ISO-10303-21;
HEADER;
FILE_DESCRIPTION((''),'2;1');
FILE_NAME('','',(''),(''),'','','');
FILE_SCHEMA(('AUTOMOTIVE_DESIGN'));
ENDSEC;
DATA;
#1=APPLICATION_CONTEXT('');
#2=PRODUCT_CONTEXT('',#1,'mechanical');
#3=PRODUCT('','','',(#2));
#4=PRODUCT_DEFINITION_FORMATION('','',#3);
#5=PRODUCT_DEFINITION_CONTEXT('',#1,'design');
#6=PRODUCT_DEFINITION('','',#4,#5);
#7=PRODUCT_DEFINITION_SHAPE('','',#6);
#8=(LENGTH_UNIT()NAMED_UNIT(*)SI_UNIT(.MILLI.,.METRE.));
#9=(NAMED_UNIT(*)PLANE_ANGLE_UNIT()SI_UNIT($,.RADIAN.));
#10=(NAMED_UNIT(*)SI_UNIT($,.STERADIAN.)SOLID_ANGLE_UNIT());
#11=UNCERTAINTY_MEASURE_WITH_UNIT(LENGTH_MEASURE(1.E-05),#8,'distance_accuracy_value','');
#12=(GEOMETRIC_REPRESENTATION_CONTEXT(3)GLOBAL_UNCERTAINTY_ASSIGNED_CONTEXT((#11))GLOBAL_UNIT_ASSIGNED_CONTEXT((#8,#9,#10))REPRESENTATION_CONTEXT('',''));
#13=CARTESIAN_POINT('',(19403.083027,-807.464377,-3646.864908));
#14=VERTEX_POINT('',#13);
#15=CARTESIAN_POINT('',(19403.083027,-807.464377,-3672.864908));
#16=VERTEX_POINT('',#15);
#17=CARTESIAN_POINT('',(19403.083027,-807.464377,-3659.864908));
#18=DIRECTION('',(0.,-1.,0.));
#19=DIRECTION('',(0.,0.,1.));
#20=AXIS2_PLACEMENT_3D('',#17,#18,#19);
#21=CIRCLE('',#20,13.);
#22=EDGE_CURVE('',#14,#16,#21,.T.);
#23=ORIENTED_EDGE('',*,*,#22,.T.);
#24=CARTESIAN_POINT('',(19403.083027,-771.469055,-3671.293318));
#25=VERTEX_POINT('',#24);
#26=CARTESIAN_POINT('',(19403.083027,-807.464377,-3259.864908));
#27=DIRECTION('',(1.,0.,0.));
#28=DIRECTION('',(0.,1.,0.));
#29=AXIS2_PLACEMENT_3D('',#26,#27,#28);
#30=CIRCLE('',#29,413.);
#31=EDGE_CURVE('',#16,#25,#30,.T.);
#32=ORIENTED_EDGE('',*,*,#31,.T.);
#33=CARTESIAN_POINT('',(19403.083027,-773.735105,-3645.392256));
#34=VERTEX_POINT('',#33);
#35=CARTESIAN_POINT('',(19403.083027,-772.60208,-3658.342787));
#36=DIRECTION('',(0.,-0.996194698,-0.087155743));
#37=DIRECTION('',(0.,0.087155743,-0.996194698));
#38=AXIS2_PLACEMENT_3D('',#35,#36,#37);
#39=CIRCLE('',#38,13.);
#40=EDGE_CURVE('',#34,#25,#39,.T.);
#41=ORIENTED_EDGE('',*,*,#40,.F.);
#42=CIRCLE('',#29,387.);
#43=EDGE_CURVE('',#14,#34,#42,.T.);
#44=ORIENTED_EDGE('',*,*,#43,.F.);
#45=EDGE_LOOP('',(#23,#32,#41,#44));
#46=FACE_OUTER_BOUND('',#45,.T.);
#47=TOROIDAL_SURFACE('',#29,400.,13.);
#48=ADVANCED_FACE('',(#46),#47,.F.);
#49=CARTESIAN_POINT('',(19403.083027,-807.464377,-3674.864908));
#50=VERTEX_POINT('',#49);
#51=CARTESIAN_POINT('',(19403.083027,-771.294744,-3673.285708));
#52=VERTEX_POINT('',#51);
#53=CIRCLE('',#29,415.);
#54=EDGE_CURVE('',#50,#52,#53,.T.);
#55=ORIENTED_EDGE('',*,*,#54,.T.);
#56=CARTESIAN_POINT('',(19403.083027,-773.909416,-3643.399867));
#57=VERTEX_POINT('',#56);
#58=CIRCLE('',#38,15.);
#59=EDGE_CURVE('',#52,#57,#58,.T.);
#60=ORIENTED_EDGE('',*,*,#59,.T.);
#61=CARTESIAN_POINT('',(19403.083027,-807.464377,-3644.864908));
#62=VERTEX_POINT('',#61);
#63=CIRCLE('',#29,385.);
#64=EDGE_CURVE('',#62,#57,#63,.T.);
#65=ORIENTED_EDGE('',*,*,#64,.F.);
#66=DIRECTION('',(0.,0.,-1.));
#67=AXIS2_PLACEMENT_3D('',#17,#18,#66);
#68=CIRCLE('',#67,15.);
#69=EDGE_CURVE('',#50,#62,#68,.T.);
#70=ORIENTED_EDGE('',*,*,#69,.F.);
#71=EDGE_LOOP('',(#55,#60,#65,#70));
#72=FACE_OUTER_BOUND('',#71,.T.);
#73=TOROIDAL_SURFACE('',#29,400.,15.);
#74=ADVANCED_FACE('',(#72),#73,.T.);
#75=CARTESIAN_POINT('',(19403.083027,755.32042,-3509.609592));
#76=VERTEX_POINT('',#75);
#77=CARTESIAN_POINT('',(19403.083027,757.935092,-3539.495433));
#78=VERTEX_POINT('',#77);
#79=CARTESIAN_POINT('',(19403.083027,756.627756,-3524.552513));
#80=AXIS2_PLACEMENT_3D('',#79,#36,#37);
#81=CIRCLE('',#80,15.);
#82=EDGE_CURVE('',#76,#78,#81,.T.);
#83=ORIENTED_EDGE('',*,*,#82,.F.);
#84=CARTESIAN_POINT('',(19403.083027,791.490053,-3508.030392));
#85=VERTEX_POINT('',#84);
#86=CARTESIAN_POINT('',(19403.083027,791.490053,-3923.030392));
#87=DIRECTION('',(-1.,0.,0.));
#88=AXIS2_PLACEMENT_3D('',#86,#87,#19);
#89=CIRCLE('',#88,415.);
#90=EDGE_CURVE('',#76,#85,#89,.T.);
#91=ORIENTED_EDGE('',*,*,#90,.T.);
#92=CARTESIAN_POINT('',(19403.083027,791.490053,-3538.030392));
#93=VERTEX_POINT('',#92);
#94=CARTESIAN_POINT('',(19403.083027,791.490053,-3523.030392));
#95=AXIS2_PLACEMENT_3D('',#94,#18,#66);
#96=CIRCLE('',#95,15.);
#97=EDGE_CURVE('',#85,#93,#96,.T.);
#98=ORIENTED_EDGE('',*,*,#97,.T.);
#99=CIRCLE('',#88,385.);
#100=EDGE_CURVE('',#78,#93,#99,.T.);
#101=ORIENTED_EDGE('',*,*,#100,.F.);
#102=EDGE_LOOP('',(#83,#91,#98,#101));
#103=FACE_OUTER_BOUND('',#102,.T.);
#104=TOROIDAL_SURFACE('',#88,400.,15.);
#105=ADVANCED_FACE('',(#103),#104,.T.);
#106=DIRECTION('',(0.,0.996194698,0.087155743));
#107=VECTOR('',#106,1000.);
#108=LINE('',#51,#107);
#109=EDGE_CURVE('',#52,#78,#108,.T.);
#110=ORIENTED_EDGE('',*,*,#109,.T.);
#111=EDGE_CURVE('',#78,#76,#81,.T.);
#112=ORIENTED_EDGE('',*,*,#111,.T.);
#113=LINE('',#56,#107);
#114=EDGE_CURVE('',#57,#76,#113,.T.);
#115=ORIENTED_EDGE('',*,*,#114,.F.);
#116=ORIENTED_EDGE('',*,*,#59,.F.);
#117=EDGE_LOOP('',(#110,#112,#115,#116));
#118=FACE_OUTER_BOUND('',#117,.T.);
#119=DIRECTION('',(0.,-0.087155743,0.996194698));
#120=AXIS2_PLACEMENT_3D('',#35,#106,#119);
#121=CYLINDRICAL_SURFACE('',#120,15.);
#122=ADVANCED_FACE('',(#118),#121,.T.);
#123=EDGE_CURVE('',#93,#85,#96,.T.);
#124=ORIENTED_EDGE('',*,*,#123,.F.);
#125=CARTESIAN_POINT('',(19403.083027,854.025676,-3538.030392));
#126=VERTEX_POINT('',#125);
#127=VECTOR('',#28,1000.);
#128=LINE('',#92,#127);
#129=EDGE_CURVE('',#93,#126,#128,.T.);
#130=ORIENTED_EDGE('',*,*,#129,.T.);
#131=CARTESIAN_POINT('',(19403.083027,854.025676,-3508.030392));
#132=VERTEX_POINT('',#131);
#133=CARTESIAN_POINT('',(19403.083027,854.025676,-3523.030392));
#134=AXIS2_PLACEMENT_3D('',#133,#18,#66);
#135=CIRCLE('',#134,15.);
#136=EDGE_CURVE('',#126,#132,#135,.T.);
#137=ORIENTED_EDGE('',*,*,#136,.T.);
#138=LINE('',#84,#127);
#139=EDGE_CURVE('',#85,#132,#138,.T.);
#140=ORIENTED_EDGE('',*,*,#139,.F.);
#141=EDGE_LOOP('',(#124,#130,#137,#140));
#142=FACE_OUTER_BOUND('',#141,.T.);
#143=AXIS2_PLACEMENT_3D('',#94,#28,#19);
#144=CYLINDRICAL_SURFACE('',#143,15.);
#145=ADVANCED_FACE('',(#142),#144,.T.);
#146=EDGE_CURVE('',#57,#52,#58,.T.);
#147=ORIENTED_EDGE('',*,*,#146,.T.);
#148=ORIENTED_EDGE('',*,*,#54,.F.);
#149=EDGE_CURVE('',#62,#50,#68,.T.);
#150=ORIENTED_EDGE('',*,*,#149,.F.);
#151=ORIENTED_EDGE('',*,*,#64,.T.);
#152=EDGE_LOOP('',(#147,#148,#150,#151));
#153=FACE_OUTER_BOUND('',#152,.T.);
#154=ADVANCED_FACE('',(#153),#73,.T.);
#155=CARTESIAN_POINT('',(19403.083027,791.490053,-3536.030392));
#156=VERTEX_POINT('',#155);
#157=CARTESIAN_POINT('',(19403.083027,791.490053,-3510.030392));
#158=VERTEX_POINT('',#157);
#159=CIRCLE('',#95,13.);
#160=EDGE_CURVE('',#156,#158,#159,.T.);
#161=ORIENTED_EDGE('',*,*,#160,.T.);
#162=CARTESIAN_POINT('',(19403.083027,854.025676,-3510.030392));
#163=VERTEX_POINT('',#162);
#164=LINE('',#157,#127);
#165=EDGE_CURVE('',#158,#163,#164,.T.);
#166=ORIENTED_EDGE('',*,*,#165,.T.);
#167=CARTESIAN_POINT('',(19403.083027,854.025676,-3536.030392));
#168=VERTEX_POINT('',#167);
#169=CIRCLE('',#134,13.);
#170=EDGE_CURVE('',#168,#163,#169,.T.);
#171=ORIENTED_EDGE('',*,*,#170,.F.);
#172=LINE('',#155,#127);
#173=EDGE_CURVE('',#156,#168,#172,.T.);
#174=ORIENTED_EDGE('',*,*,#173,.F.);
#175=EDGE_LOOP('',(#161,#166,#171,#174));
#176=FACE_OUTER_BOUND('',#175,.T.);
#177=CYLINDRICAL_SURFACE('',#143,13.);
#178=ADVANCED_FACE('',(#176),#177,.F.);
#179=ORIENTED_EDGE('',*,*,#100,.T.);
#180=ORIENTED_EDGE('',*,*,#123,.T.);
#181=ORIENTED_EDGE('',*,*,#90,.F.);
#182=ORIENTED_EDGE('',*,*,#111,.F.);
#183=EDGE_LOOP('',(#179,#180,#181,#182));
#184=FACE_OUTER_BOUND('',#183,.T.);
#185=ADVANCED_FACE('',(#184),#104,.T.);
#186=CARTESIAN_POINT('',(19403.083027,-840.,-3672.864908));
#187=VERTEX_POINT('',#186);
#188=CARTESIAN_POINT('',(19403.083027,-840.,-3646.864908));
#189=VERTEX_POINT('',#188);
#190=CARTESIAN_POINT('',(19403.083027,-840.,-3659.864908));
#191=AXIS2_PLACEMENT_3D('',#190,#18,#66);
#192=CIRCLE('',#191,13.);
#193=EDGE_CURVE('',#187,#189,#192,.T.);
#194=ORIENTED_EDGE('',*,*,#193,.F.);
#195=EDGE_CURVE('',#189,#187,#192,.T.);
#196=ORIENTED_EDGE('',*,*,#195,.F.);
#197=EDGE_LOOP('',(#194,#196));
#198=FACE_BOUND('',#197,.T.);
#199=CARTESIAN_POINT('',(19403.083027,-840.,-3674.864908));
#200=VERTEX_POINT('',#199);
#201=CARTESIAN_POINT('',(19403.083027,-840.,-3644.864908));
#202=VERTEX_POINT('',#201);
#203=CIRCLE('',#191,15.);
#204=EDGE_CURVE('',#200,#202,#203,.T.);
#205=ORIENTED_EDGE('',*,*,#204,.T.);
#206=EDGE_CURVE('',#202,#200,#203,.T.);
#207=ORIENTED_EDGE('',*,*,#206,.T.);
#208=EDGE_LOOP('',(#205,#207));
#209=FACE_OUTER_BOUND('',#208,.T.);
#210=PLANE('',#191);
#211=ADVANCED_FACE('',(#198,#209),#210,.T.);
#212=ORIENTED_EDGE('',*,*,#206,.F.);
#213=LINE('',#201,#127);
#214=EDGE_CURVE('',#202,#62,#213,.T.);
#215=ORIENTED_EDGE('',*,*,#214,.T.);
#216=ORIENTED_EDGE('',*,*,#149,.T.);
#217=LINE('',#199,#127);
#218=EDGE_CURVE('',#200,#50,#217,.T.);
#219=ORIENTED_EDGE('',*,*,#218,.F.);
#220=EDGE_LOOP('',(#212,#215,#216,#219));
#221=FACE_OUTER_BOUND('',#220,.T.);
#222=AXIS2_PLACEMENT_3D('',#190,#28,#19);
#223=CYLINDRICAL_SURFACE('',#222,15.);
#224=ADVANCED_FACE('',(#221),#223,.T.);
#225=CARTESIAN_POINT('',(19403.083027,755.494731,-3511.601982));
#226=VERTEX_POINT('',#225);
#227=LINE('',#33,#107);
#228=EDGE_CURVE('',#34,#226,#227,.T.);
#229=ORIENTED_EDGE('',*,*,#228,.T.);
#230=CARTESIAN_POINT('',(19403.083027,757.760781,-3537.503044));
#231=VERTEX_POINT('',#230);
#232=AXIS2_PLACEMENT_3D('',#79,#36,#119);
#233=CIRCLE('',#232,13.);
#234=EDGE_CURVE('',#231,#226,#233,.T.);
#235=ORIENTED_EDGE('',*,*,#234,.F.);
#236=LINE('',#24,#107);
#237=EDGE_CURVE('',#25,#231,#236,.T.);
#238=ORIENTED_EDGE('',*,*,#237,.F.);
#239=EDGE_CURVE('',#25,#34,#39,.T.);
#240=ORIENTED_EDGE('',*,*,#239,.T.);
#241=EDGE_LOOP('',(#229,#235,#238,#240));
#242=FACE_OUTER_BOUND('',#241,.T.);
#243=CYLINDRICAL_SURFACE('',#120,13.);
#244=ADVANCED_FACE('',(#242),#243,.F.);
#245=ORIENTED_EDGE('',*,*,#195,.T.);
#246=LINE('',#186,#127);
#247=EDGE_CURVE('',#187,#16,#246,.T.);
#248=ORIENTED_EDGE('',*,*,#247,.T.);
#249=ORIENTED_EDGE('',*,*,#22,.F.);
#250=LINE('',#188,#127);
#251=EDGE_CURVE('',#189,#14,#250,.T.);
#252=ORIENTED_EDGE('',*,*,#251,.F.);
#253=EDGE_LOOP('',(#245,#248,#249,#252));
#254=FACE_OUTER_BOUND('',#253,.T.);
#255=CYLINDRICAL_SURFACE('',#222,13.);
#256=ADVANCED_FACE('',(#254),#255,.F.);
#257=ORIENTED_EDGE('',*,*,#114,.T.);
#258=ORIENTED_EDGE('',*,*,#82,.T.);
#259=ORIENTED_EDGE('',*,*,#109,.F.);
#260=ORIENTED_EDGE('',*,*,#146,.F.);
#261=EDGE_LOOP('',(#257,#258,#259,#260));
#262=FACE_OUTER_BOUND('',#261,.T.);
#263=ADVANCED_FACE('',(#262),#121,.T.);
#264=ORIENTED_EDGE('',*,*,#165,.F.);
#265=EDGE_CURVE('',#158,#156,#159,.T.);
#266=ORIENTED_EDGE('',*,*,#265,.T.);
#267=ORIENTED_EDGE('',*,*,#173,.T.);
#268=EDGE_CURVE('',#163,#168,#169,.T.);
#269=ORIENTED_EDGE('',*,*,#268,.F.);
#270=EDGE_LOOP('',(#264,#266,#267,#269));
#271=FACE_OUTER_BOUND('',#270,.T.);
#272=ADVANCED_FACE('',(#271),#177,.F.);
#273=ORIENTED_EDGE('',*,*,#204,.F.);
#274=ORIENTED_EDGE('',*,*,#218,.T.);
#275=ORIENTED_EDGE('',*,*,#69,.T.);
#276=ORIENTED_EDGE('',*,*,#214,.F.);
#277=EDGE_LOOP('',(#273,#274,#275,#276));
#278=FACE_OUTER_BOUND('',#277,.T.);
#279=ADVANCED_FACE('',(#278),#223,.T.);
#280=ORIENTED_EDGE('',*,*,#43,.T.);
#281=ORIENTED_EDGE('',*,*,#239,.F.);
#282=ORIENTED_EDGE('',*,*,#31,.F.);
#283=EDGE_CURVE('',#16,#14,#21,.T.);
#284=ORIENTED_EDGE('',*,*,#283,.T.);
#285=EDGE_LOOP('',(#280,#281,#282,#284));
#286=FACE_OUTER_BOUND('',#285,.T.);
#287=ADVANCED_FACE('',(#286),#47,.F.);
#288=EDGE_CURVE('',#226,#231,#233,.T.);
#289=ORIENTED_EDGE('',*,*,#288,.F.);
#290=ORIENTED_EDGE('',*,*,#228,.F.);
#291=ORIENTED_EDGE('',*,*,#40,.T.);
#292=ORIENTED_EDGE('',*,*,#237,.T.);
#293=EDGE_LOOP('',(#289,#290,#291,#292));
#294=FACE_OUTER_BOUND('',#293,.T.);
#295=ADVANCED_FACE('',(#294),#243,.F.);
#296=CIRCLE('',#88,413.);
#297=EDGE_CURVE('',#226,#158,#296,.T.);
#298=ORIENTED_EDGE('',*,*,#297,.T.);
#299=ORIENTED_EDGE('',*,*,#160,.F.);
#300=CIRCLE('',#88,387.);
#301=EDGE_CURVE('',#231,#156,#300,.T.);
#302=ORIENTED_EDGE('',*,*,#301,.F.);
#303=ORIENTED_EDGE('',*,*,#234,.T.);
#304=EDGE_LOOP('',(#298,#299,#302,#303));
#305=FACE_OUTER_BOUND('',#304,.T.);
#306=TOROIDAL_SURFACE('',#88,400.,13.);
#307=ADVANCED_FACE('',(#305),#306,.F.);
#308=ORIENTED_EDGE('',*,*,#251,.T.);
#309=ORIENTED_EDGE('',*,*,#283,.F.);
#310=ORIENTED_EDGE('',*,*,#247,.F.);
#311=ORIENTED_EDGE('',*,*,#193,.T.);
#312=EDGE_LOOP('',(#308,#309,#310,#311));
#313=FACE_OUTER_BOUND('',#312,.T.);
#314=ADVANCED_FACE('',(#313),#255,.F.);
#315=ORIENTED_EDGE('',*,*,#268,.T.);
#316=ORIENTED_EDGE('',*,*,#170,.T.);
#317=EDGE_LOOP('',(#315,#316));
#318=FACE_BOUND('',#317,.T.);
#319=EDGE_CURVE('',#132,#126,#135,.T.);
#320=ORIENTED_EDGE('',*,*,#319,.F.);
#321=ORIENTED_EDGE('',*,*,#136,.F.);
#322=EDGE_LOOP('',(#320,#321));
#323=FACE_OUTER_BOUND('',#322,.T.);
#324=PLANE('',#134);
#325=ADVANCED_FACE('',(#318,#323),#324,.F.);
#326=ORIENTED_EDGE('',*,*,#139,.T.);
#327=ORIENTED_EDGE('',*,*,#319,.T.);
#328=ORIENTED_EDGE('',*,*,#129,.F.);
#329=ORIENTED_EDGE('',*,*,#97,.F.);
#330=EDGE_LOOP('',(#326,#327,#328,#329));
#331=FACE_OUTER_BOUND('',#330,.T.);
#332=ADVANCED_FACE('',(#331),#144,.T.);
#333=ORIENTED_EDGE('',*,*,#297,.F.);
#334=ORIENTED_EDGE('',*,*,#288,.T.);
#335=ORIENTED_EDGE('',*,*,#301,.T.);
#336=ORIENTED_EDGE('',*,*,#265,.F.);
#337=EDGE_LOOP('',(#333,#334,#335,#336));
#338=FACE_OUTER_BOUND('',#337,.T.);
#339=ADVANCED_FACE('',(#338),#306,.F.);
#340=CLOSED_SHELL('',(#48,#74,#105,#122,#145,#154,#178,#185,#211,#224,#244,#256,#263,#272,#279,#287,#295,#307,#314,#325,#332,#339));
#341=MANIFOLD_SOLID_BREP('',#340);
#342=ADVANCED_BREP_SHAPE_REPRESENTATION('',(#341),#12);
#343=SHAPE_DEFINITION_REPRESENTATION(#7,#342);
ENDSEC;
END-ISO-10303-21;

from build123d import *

# Parameters (mm, degrees)
SWEEP_THIN1_PROFILE_R   = 15
SWEEP_THIN1_PROFILE_R_2 = 13


with BuildPart() as part:
    # Sweep-Thin1: sweep along a curve in space
    with BuildLine() as sweep_thin1_path:
        Line((19403.083026604, -840, -3659.86490803), (19403.083026604, -807.464377163, -3659.86490803))
        ThreePointArc((19403.083026604, -807.464377163, -3659.86490803), (19403.083026604, -790.016622217, -3659.484196663), (19403.083026604, -772.602080064, -3658.342787267))
        Line((19403.083026604, -772.602080064, -3658.342787267), (19403.083026604, 756.627756068, -3524.552512679))
        ThreePointArc((19403.083026604, 756.627756068, -3524.552512679), (19403.083026604, 774.042298221, -3523.411103283), (19403.083026604, 791.490053167, -3523.030391916))
        Line((19403.083026604, 791.490053167, -3523.030391916), (19403.083026604, 854.025676004, -3523.030391916))
    # Sweep-Thin1 profile (on start of the path) → Sweep-Thin1 (sweep)
    with BuildSketch(Plane(origin=(19403.083026604, -840, -3659.86490803), x_dir=(0, 0, 1), z_dir=(0, 1, 0))):
        Circle(SWEEP_THIN1_PROFILE_R)
        Circle(SWEEP_THIN1_PROFILE_R_2, mode=Mode.SUBTRACT)
    sweep(path=sweep_thin1_path.line)


solid = part.part
